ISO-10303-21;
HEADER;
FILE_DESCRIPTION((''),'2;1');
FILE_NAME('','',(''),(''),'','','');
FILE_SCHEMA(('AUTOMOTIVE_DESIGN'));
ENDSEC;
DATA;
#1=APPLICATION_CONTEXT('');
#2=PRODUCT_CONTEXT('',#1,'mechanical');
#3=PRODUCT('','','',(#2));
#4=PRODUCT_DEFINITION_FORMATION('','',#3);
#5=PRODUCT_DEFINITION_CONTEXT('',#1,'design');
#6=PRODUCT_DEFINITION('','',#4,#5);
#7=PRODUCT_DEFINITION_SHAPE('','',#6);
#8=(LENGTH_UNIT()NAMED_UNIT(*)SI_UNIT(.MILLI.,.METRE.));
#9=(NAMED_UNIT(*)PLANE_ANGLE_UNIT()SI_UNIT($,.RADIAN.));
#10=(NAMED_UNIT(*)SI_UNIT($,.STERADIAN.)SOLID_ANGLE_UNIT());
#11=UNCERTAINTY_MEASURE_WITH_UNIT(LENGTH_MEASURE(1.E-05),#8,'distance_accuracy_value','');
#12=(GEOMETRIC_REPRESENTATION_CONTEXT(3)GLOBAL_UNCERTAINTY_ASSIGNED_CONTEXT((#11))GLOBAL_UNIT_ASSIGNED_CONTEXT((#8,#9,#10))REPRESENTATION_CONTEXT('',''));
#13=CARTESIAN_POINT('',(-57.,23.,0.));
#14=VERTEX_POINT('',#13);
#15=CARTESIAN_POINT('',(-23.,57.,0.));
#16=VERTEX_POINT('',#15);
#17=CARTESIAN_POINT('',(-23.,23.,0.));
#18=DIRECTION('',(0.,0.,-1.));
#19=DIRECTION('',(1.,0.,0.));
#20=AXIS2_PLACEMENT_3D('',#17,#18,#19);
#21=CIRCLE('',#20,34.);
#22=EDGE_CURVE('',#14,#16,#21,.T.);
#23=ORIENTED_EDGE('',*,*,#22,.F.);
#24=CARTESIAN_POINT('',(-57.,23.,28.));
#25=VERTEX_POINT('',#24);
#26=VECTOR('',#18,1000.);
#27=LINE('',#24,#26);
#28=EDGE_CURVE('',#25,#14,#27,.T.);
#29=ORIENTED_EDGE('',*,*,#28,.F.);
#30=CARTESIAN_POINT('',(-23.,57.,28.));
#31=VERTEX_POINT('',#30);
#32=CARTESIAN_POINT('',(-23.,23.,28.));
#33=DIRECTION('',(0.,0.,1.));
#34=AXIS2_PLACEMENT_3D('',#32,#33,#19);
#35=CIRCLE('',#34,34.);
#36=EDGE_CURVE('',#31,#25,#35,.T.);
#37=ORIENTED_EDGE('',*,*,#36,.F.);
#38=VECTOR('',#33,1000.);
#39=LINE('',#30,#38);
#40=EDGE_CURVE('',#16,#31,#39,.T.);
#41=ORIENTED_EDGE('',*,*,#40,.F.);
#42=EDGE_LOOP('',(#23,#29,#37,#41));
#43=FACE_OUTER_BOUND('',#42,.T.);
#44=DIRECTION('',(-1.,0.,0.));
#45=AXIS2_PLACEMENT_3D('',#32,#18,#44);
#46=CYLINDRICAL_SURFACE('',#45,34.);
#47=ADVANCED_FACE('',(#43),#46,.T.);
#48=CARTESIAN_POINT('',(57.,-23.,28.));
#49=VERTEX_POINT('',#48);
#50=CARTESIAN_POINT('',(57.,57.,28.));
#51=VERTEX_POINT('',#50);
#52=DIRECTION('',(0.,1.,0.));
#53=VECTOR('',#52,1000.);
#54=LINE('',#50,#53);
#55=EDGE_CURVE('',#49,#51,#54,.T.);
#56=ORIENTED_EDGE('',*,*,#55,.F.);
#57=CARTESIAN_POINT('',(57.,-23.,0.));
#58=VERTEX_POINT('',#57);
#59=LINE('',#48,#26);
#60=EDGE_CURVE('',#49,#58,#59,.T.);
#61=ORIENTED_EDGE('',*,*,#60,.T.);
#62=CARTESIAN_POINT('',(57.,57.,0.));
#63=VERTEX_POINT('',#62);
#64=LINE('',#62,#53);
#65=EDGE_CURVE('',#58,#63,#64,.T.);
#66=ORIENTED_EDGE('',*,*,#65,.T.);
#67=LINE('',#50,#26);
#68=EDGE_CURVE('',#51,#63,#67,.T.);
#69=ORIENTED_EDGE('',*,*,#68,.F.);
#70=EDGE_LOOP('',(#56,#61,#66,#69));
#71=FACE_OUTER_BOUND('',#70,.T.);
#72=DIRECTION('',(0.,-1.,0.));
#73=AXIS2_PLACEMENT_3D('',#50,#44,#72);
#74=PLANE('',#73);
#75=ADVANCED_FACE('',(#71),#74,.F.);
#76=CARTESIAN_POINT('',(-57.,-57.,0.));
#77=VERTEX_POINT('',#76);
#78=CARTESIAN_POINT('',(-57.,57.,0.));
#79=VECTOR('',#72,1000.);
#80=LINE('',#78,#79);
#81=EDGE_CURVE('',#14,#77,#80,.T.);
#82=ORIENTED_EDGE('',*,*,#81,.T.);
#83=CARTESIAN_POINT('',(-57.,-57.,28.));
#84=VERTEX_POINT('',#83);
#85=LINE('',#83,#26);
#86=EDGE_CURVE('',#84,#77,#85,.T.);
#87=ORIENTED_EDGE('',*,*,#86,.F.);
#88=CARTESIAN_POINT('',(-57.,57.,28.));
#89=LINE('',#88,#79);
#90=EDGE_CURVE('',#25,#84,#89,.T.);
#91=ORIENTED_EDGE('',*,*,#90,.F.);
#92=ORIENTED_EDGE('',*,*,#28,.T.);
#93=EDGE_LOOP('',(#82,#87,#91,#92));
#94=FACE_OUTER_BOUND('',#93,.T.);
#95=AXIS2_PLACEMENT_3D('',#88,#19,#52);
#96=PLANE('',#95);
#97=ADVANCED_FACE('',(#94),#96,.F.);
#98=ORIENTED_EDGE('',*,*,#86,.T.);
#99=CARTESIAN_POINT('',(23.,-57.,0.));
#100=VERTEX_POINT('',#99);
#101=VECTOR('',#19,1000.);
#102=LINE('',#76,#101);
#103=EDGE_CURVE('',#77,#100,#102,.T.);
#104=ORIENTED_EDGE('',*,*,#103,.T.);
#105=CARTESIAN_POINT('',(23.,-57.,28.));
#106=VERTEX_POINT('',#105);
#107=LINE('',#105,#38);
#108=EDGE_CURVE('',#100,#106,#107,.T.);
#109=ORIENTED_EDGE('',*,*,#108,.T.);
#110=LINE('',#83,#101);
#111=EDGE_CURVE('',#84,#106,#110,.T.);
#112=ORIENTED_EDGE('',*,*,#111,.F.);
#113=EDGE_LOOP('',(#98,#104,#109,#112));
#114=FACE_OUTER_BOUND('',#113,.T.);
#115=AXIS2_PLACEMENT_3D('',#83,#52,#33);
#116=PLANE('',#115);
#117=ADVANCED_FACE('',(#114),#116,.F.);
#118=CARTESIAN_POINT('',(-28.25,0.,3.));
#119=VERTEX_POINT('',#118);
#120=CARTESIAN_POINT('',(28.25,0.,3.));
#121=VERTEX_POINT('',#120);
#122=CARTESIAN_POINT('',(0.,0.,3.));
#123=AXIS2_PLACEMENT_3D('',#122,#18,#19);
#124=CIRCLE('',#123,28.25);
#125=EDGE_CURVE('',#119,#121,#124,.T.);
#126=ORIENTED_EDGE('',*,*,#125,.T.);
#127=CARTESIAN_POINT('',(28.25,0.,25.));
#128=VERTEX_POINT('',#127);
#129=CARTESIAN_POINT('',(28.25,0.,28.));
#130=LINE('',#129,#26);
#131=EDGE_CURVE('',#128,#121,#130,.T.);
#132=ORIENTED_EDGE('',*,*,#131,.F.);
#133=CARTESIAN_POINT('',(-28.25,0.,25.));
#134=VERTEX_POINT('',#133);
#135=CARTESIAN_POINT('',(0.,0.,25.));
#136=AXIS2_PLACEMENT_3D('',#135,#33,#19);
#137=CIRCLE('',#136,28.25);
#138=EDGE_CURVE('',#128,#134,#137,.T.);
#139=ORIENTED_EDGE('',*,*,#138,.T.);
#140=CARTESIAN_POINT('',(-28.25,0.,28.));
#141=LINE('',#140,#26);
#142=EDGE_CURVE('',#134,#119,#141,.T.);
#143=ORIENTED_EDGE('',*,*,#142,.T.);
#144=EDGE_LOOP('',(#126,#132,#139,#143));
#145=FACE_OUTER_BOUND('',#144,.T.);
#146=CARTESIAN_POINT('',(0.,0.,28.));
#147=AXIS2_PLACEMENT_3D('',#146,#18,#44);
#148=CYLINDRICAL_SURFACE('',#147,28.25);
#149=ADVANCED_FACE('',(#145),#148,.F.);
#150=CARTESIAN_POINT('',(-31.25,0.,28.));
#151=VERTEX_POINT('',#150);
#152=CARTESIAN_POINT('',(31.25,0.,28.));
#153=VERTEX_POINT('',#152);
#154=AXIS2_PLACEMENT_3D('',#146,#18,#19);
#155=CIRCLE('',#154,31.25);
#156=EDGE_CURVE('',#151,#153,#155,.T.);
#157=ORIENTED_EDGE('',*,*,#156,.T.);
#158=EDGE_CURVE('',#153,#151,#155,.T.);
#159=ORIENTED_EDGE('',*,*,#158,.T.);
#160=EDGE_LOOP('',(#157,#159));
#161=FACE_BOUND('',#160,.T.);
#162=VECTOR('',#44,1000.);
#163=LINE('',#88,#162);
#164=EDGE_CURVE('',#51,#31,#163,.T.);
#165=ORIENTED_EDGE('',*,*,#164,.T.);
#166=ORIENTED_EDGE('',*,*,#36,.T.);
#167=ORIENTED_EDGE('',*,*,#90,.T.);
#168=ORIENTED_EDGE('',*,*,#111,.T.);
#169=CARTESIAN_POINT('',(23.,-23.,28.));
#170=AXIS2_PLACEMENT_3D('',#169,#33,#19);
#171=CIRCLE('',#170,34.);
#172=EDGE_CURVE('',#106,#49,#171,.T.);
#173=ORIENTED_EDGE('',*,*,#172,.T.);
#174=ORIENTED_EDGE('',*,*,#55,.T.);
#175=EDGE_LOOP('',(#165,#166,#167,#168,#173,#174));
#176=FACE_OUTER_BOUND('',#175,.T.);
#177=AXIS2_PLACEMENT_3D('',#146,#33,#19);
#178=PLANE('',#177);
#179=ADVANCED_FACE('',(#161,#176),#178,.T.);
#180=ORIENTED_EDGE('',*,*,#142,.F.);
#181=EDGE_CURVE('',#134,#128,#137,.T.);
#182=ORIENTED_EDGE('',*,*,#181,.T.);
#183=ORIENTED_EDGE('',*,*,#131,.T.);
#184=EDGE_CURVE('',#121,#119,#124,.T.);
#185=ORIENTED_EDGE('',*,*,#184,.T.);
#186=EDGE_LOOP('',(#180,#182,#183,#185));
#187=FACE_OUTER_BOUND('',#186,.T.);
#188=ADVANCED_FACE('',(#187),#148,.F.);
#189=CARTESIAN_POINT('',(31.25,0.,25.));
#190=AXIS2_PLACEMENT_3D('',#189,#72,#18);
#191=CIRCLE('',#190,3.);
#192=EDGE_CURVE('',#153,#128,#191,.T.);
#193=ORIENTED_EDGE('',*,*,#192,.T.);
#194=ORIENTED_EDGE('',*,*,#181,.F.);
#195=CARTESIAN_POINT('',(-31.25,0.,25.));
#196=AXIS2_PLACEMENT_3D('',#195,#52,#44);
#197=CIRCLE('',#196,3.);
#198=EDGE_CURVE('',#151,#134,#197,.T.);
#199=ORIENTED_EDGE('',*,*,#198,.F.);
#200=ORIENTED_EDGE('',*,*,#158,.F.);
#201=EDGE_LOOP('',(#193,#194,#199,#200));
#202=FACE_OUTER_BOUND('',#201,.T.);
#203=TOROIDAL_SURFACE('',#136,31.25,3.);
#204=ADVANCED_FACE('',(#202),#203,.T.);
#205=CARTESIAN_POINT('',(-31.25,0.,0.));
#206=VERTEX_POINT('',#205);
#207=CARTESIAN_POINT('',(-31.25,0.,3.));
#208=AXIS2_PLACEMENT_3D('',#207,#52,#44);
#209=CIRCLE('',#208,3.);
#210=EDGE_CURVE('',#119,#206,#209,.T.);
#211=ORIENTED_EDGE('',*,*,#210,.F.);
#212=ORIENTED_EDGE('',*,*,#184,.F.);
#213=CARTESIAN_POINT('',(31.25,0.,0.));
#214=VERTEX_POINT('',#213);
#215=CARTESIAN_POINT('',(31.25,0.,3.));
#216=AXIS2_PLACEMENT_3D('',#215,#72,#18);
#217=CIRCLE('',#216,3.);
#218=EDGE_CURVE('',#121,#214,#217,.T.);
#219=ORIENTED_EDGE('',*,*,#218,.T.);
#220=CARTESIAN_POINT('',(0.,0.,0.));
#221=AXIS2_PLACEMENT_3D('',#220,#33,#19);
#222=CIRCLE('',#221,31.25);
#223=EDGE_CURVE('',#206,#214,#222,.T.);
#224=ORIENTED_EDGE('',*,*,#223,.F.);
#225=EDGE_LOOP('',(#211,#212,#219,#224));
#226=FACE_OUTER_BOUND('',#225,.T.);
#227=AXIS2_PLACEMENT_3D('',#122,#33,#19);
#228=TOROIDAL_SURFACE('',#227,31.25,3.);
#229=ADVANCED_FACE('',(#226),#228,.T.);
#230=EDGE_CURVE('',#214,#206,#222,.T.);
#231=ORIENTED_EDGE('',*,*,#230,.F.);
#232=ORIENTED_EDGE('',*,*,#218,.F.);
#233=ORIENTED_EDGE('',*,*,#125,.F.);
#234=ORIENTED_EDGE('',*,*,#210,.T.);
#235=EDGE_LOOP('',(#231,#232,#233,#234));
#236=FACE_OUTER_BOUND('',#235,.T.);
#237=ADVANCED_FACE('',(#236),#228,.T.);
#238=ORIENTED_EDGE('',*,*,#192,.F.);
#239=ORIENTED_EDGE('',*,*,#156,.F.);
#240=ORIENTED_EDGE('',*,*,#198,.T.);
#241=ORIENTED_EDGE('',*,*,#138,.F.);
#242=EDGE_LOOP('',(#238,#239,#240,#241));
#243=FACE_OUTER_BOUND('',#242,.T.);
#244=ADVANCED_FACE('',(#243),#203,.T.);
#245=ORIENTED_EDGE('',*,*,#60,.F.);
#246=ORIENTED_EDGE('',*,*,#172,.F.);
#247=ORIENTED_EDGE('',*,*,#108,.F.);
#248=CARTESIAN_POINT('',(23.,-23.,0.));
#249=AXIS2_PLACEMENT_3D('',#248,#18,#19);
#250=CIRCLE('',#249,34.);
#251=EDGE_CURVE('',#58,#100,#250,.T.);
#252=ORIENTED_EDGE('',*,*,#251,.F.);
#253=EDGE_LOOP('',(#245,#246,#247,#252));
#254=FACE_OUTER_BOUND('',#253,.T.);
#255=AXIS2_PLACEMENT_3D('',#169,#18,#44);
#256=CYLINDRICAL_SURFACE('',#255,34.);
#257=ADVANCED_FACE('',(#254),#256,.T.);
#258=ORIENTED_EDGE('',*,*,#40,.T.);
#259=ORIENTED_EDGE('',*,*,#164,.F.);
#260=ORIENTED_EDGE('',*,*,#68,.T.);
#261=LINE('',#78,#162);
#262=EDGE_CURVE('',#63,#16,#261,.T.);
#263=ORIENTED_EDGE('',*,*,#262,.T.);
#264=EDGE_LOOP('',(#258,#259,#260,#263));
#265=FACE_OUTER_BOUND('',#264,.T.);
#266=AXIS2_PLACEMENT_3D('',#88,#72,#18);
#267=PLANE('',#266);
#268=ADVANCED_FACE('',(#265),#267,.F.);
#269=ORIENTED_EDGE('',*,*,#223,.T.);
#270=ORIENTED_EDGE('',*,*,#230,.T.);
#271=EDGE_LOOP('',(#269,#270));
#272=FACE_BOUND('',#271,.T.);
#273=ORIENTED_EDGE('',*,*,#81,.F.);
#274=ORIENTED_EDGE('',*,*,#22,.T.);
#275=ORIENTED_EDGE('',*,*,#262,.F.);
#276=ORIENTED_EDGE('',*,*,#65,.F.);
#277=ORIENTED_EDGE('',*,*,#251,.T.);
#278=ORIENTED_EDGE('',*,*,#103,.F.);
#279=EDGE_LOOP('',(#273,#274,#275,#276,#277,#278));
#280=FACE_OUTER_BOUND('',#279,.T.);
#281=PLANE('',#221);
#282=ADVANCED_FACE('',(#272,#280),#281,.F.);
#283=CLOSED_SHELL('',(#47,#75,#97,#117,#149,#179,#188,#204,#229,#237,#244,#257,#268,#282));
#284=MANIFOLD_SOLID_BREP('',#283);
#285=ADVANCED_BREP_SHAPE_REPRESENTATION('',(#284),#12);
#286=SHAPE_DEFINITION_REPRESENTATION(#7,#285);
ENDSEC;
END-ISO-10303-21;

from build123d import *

# Parameters (mm, degrees)
SKETCH1_W           = 114
SKETCH1_H           = 114
SKETCH1_R           = 28.25
BOSS_EXTRUDE1_DEPTH = 28
FILLET1_R           = 3
FILLET3_R           = 34


with BuildPart() as part:
    # Sketch1 → Boss-Extrude1 (new body)
    with BuildSketch(Plane.XY):
        Rectangle(SKETCH1_W, SKETCH1_H)
        Circle(SKETCH1_R, mode=Mode.SUBTRACT)
    extrude(amount=BOSS_EXTRUDE1_DEPTH)

    # Fillet1
    fillet1_edges = [part.edges().sort_by_distance(p)[0] for p in [
        (-28.25, 0, 0),
        (-28.25, 0, 28),
    ]]
    fillet(fillet1_edges, radius=FILLET1_R)

    # Fillet3
    fillet3_edges = [part.edges().sort_by_distance(p)[0] for p in [
        (-57, 57, 14),
        (57, -57, 14),
    ]]
    fillet(fillet3_edges, radius=FILLET3_R)


solid = part.part
